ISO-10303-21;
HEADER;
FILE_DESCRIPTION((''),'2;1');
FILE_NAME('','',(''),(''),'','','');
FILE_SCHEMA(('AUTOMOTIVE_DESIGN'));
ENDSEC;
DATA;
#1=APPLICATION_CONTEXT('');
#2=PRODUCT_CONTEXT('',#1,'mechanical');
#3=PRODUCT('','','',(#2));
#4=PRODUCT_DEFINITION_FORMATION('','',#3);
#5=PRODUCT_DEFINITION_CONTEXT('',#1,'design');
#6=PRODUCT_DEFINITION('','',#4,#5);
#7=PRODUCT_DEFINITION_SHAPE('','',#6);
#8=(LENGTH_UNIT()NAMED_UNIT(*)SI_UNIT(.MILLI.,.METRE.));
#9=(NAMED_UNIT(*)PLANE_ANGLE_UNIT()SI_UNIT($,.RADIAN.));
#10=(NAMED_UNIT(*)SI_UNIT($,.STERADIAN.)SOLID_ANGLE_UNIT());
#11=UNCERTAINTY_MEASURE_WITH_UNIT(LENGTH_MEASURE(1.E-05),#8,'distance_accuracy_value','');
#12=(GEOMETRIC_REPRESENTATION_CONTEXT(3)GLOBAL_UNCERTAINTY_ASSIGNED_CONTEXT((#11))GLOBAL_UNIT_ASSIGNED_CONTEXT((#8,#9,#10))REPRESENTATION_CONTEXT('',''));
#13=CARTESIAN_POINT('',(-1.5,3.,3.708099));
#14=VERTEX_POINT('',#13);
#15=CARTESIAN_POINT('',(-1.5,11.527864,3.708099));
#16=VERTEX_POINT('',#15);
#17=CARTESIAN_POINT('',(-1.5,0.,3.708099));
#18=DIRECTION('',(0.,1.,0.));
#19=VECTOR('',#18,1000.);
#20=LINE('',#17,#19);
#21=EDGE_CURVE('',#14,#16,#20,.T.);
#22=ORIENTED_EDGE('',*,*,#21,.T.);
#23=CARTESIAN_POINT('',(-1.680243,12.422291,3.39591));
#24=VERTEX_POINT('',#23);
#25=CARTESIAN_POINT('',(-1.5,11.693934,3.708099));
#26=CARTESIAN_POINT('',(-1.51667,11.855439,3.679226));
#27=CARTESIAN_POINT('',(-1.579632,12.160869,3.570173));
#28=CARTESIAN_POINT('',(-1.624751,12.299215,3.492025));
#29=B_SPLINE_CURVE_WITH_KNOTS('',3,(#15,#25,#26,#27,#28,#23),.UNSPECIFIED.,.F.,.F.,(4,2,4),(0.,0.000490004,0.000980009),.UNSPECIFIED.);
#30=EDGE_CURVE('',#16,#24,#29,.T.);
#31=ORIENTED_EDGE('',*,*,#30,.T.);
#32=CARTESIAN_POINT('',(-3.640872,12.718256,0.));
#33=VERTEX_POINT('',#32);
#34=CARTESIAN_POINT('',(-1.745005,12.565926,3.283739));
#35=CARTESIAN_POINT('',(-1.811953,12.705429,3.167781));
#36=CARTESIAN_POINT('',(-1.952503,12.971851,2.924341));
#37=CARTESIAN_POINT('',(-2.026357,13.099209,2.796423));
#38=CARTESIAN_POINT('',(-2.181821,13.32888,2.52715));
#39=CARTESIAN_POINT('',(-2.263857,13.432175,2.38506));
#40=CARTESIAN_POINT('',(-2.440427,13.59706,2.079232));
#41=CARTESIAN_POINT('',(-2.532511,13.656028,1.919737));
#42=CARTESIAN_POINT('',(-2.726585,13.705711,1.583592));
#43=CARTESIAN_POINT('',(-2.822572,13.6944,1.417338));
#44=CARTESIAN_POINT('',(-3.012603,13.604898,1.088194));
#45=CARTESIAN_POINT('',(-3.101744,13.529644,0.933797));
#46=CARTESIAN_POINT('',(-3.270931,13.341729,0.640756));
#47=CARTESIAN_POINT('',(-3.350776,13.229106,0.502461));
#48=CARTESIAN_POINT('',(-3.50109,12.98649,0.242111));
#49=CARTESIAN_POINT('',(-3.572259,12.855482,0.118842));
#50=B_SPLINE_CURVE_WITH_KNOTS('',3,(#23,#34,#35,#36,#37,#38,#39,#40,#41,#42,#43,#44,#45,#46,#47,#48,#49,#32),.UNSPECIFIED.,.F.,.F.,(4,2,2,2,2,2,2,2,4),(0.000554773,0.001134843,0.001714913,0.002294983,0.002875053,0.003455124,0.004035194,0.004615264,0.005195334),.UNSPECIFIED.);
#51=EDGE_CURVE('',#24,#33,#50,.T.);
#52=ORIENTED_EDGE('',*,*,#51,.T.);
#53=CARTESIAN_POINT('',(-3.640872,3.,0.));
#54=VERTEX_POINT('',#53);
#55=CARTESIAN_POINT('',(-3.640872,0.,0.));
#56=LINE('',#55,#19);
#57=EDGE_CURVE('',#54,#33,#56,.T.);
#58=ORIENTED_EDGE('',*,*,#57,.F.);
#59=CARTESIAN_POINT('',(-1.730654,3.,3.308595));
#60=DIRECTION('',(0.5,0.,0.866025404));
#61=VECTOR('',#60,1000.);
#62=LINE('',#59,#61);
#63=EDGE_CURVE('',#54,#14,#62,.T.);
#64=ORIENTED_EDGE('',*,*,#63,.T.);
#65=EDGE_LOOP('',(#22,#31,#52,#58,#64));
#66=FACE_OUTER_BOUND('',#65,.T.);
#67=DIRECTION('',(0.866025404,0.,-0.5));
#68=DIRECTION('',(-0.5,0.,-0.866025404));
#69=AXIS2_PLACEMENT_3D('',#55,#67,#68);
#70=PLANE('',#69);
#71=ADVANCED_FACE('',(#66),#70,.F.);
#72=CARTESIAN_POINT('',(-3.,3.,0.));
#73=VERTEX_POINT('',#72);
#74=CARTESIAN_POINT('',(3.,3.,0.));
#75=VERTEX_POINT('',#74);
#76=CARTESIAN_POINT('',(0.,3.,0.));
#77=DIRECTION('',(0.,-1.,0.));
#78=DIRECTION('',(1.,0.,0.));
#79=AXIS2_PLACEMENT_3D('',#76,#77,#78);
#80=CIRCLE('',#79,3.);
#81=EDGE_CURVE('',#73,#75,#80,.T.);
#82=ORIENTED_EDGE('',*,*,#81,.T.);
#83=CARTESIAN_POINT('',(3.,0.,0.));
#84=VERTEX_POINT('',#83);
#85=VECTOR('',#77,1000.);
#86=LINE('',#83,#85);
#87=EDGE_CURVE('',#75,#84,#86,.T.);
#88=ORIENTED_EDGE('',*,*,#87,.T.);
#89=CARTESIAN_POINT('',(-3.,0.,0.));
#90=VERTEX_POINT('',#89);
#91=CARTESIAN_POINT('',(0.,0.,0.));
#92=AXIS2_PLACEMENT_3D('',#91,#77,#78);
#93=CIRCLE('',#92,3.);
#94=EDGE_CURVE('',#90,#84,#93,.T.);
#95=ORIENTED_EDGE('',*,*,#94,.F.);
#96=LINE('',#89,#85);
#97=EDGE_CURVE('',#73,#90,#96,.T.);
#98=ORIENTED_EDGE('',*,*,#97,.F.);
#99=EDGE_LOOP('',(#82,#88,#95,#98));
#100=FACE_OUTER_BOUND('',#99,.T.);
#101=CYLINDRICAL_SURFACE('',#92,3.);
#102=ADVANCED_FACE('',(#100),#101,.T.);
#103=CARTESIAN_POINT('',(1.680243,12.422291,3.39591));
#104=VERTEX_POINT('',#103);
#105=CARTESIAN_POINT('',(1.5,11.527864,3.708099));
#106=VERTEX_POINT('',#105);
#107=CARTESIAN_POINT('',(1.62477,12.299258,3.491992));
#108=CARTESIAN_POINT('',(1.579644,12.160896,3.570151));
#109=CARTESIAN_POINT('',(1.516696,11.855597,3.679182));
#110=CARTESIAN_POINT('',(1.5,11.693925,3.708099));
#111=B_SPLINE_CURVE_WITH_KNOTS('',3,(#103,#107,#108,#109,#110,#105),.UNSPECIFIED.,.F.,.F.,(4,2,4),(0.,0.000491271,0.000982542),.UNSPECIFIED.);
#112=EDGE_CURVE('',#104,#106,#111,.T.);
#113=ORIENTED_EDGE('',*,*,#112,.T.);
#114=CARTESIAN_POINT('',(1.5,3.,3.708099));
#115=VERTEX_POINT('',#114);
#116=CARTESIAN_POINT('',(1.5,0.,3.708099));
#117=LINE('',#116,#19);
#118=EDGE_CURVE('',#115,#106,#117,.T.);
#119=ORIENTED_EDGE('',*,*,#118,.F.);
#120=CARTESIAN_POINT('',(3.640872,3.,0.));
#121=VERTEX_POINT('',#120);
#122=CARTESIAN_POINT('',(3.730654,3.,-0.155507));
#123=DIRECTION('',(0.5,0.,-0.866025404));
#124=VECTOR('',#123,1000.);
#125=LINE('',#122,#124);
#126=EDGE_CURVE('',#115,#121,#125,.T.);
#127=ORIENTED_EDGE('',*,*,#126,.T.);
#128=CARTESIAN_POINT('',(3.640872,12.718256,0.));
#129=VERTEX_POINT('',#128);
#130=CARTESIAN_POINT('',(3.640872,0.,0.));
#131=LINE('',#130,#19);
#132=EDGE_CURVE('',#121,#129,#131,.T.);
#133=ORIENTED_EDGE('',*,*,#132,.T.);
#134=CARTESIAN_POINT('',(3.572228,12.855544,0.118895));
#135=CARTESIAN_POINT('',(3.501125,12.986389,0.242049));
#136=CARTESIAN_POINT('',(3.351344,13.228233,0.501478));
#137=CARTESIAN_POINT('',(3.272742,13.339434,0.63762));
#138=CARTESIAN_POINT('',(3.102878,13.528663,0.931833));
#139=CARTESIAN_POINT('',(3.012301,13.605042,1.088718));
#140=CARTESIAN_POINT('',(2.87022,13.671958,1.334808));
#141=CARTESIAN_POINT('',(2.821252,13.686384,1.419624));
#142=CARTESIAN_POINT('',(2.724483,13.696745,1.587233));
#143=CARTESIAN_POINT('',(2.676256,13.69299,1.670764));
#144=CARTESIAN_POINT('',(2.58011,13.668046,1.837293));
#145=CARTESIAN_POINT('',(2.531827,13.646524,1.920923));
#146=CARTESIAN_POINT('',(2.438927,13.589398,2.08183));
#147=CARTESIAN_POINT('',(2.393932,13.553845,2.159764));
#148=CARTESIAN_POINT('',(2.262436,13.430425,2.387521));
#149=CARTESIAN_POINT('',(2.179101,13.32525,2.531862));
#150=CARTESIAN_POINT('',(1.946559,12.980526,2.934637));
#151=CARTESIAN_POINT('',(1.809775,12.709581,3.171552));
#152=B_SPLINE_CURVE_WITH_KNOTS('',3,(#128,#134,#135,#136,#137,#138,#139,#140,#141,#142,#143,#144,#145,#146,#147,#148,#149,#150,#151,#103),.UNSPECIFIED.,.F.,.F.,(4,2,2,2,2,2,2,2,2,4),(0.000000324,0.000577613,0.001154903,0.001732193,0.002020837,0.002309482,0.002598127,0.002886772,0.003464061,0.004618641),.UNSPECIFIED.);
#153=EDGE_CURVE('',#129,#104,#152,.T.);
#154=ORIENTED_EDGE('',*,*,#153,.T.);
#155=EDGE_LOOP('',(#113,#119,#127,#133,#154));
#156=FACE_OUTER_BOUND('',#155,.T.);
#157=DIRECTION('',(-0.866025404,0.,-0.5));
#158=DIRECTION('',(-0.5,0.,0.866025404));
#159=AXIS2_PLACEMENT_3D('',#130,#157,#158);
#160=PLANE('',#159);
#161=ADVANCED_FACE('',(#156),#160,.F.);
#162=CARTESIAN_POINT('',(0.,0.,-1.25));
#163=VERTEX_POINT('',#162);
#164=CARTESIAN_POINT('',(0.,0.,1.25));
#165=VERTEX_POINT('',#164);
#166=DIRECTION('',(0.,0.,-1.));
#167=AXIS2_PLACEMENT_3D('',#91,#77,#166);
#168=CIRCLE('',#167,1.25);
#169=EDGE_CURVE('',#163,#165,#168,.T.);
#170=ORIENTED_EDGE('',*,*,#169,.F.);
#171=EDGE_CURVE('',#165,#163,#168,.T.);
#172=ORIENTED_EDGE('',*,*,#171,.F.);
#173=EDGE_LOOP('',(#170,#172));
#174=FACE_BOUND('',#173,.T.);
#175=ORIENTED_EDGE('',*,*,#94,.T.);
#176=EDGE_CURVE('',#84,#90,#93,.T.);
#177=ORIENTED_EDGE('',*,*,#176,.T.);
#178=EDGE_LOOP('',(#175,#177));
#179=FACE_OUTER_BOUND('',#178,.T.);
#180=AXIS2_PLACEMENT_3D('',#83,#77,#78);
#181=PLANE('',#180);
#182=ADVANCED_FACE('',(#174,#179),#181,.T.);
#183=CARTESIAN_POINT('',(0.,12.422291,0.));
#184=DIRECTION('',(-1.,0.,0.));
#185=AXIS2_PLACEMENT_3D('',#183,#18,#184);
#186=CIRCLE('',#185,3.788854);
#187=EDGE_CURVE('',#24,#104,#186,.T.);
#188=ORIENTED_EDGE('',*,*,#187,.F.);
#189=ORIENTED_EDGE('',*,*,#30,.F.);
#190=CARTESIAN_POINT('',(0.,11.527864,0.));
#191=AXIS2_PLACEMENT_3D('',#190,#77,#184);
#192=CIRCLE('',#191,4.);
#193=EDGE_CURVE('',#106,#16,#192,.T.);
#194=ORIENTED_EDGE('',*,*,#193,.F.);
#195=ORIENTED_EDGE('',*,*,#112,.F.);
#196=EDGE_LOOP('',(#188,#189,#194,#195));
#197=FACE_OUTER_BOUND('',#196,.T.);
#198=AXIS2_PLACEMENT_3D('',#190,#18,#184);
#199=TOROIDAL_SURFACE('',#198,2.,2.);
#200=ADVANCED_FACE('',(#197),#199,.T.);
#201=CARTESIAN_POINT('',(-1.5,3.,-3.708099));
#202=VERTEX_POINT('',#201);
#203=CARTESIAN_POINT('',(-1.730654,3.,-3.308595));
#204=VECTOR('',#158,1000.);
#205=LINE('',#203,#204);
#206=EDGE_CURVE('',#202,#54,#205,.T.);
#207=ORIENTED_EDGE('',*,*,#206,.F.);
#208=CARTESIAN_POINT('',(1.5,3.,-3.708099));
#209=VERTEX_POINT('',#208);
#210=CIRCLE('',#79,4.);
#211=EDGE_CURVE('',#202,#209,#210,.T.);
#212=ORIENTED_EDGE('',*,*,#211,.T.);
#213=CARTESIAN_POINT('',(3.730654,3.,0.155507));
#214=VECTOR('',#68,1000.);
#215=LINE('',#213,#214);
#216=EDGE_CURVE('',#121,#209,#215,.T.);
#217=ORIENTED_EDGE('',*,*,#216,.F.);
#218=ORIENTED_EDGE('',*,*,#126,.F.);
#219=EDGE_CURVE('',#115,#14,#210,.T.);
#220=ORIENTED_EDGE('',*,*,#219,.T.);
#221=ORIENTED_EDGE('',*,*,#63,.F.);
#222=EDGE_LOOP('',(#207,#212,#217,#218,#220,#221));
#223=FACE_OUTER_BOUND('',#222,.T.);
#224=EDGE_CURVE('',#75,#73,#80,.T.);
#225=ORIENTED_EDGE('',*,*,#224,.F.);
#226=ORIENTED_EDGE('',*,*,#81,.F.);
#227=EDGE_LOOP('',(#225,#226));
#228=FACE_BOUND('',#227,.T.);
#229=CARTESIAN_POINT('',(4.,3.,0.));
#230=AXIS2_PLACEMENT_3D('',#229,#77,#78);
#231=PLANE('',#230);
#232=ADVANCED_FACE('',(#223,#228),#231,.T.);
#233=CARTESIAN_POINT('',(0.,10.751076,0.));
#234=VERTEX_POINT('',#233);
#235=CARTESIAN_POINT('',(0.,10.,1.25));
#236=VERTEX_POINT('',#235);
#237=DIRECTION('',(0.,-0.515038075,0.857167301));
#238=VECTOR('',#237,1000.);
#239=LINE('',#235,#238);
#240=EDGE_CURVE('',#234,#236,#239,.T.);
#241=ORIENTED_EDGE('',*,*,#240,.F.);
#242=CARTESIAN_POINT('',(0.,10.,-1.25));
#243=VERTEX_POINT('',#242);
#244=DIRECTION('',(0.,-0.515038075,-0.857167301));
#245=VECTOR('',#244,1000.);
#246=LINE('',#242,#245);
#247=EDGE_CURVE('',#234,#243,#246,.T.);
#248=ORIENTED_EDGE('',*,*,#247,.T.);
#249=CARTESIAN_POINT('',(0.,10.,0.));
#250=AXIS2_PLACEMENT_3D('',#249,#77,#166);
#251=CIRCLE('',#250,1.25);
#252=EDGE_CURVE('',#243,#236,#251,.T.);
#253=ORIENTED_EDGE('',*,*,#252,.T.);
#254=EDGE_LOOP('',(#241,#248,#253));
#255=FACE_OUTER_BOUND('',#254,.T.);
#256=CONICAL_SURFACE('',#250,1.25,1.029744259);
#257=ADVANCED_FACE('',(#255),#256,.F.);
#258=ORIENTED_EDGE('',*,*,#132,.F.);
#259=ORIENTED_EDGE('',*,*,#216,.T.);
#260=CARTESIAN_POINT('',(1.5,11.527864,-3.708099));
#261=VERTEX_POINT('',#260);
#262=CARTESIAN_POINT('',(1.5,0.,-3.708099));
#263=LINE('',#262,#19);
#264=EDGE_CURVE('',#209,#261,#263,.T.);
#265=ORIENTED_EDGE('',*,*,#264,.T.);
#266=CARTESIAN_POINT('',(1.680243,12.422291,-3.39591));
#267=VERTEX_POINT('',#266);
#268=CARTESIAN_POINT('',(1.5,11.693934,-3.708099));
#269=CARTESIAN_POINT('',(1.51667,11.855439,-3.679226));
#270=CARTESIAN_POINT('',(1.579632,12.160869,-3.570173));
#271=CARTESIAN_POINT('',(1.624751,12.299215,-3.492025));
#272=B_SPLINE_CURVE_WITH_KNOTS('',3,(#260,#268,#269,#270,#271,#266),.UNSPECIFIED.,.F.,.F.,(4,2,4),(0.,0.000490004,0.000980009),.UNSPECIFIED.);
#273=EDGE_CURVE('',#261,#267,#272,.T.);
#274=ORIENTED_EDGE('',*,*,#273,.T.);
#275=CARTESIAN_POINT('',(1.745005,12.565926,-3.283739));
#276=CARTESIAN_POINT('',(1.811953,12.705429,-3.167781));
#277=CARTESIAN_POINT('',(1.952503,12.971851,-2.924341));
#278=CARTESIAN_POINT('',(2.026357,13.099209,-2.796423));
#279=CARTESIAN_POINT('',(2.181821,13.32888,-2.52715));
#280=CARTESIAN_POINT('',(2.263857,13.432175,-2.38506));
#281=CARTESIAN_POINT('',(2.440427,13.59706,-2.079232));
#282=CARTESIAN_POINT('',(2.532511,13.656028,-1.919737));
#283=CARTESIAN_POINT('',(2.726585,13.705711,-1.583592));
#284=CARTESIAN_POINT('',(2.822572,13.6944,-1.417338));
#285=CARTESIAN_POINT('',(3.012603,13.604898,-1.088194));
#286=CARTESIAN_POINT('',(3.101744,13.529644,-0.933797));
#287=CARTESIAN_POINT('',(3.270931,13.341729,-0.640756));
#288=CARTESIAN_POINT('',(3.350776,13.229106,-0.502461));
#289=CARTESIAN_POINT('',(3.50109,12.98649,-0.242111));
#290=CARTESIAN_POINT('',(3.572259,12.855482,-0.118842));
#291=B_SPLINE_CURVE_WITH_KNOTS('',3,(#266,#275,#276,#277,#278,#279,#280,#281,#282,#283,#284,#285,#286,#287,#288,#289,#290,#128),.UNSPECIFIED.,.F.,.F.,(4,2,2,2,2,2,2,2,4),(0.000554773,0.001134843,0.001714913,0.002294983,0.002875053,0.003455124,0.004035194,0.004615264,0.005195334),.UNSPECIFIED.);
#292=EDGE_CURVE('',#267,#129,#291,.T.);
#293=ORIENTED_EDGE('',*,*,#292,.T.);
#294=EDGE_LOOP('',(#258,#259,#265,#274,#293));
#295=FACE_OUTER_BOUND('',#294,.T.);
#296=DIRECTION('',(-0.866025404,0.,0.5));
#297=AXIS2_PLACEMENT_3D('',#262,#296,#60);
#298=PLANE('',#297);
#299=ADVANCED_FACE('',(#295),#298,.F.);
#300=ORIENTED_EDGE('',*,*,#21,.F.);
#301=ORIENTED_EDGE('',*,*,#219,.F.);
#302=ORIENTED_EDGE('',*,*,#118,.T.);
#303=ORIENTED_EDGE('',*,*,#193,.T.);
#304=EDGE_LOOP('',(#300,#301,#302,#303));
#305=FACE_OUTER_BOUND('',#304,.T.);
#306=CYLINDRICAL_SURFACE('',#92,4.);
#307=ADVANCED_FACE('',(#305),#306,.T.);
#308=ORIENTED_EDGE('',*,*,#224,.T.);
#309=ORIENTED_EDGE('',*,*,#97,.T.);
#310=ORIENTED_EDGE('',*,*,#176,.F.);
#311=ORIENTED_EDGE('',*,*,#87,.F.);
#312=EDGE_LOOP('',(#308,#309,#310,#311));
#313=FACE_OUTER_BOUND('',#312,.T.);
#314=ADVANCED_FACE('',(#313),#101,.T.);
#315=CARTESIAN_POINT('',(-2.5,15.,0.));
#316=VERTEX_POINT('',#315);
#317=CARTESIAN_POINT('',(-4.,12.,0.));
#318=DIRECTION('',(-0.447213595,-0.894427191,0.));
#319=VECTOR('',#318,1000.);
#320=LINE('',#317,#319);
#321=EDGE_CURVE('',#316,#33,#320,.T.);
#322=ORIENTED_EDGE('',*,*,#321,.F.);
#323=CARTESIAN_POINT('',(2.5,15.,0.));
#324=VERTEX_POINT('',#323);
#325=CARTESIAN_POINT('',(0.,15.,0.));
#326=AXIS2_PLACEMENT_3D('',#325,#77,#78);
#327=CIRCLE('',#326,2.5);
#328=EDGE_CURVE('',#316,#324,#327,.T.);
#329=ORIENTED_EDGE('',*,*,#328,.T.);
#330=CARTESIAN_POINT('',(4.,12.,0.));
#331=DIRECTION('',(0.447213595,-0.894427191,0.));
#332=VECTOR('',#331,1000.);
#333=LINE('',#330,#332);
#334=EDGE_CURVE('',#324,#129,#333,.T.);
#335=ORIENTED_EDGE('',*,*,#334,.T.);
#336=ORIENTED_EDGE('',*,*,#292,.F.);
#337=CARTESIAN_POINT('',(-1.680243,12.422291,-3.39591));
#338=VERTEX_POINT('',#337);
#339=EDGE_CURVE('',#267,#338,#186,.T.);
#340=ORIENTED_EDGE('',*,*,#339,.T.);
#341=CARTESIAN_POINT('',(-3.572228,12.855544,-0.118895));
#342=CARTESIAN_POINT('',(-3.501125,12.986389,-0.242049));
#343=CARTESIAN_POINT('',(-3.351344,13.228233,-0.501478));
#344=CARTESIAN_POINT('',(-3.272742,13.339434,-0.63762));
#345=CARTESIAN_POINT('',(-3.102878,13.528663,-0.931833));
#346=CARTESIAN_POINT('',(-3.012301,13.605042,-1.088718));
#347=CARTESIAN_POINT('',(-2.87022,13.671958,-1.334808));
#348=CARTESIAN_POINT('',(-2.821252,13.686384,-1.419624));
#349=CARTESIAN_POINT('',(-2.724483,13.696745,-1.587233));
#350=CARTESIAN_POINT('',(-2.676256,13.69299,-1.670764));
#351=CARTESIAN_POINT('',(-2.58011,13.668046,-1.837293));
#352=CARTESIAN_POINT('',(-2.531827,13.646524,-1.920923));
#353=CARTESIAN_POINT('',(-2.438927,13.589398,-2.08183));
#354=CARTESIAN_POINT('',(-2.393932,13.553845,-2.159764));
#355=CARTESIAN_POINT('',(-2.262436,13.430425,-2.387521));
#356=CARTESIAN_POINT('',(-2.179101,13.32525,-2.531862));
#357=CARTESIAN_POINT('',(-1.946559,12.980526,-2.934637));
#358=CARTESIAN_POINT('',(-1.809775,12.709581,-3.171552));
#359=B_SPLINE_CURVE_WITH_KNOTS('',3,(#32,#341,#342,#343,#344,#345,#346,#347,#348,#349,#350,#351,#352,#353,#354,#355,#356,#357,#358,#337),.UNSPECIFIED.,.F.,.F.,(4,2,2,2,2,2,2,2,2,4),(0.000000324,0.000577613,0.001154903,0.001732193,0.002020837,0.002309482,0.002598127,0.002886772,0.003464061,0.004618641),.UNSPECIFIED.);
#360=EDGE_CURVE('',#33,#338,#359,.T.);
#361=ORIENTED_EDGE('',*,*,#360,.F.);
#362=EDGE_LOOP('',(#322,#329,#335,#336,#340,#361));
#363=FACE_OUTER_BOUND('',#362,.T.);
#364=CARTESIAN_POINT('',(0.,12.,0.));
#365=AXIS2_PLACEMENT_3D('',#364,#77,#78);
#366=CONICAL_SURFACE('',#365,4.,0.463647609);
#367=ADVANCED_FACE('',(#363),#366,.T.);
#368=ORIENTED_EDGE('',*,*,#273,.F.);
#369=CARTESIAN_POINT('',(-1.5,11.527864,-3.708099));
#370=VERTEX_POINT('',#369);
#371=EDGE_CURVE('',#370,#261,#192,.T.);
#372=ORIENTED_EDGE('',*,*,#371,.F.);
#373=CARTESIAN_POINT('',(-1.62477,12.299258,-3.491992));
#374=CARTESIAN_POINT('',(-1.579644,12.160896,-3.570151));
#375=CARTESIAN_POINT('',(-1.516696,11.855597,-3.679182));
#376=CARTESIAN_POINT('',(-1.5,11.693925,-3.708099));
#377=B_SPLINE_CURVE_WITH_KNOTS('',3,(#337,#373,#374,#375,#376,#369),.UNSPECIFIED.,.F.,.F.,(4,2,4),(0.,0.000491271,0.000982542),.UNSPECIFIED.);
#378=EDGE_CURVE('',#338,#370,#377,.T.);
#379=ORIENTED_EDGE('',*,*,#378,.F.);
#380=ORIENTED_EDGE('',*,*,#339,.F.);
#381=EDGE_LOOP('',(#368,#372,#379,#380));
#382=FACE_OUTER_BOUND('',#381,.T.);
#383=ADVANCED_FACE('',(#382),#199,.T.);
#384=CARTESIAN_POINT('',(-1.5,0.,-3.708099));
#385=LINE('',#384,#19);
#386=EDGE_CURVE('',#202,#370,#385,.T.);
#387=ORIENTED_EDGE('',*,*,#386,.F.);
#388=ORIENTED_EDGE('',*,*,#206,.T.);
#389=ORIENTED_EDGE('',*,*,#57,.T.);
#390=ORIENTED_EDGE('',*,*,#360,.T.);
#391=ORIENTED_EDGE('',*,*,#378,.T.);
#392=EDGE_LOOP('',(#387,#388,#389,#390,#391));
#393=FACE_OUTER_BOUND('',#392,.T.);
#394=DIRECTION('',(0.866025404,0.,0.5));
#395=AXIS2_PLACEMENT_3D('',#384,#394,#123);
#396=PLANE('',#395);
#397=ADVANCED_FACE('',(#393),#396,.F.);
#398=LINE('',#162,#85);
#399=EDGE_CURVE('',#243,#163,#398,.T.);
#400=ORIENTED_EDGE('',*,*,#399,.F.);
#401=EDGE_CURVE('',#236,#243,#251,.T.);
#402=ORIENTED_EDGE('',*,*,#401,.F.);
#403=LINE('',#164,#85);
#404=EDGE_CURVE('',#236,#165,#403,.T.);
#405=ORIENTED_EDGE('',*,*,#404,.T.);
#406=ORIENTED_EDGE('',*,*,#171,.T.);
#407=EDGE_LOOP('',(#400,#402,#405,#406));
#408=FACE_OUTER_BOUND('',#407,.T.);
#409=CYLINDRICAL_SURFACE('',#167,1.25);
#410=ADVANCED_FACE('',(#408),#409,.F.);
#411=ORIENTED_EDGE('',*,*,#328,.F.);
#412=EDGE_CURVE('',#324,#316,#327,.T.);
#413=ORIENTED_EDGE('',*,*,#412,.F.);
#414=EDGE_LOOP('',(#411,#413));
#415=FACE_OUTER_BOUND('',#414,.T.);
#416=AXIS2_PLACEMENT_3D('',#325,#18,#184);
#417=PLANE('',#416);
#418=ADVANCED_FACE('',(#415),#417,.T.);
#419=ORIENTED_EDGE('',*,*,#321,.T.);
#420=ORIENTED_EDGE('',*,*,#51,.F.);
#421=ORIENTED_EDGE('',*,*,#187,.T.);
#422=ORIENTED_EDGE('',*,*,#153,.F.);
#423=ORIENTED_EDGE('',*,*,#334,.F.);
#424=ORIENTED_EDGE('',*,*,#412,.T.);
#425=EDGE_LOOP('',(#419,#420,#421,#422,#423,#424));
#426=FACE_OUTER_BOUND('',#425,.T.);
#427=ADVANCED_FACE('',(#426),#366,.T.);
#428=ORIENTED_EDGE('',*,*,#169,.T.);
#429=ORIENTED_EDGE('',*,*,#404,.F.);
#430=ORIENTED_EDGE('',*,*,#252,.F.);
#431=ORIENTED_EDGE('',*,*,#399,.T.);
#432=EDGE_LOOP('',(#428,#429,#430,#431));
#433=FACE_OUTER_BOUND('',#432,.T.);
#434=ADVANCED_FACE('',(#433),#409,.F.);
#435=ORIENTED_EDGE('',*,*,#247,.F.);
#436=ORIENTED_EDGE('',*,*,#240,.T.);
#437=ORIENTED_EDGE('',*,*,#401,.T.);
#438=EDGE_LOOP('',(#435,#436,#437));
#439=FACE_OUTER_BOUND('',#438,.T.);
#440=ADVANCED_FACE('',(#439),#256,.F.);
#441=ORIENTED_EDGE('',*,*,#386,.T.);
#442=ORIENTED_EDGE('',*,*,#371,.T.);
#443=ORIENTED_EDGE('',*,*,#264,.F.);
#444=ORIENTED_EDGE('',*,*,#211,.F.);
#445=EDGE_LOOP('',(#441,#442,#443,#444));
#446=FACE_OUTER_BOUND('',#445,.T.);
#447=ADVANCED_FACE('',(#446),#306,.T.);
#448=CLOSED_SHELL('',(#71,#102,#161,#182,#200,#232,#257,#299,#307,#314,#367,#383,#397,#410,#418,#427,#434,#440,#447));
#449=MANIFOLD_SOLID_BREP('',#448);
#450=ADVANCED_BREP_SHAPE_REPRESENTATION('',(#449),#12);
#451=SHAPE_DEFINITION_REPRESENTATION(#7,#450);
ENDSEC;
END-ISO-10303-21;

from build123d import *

# Parameters (mm, degrees)
M3_TAPPED_HOLE1_D     = 2.5
M3_TAPPED_HOLE1_DEPTH = 10
M3_TAPPED_HOLE1_TIP   = 0.751075774
CUT_EXTRUDE1_DEPTH    = 17.031219542
FILLET1_R             = 2


with BuildPart() as part:
    # Sketch1 → Revolve1 (revolve)
    with BuildSketch(Plane.XY):
        Polygon((0, 0), (0, 15), (2.5, 15), (4, 12), (4, 3), (3, 3), (3, 0), align=None)
    revolve(axis=Axis((0, 0, 0), (0, 1, 0)))

    # M3 Tapped Hole1
    with Locations(Plane(origin=(0, 0, 0), x_dir=(-1, 0, 0), z_dir=(0, -1, 0))):
        with Locations((0, 0)):
            Hole(M3_TAPPED_HOLE1_D / 2, depth=M3_TAPPED_HOLE1_DEPTH)
            with Locations((0, 0, -(M3_TAPPED_HOLE1_DEPTH + M3_TAPPED_HOLE1_TIP / 2))):  # 118° drill point
                Cone(0, M3_TAPPED_HOLE1_D / 2, M3_TAPPED_HOLE1_TIP, mode=Mode.SUBTRACT)

    # Sketch4 → Cut-Extrude1 (cut, through all)
    with BuildSketch(Plane(origin=(0, 15, 0), x_dir=(1, 0, 0), z_dir=(0, 1, 0))):
        with BuildLine():
            Line((-1.5, 3.708099244), (-3.640872096, 0))
            Line((-3.640872096, 0), (-1.5, -3.708099244))
            ThreePointArc((-1.5, -3.708099244), (-4, 0), (-1.5, 3.708099244))
        make_face()
        with BuildLine():
            Line((1.5, 3.708099244), (3.640872096, 0))
            Line((3.640872096, 0), (1.5, -3.708099244))
            ThreePointArc((1.5, -3.708099244), (4, 0), (1.5, 3.708099244))
        make_face()
    extrude(amount=-CUT_EXTRUDE1_DEPTH, mode=Mode.SUBTRACT)

    # Fillet1
    fillet1_edges = [part.edges().sort_by_distance(p)[0] for p in [
        (0, 12, -4),
        (0, 12, 4),
    ]]
    fillet(fillet1_edges, radius=FILLET1_R)


solid = part.part
